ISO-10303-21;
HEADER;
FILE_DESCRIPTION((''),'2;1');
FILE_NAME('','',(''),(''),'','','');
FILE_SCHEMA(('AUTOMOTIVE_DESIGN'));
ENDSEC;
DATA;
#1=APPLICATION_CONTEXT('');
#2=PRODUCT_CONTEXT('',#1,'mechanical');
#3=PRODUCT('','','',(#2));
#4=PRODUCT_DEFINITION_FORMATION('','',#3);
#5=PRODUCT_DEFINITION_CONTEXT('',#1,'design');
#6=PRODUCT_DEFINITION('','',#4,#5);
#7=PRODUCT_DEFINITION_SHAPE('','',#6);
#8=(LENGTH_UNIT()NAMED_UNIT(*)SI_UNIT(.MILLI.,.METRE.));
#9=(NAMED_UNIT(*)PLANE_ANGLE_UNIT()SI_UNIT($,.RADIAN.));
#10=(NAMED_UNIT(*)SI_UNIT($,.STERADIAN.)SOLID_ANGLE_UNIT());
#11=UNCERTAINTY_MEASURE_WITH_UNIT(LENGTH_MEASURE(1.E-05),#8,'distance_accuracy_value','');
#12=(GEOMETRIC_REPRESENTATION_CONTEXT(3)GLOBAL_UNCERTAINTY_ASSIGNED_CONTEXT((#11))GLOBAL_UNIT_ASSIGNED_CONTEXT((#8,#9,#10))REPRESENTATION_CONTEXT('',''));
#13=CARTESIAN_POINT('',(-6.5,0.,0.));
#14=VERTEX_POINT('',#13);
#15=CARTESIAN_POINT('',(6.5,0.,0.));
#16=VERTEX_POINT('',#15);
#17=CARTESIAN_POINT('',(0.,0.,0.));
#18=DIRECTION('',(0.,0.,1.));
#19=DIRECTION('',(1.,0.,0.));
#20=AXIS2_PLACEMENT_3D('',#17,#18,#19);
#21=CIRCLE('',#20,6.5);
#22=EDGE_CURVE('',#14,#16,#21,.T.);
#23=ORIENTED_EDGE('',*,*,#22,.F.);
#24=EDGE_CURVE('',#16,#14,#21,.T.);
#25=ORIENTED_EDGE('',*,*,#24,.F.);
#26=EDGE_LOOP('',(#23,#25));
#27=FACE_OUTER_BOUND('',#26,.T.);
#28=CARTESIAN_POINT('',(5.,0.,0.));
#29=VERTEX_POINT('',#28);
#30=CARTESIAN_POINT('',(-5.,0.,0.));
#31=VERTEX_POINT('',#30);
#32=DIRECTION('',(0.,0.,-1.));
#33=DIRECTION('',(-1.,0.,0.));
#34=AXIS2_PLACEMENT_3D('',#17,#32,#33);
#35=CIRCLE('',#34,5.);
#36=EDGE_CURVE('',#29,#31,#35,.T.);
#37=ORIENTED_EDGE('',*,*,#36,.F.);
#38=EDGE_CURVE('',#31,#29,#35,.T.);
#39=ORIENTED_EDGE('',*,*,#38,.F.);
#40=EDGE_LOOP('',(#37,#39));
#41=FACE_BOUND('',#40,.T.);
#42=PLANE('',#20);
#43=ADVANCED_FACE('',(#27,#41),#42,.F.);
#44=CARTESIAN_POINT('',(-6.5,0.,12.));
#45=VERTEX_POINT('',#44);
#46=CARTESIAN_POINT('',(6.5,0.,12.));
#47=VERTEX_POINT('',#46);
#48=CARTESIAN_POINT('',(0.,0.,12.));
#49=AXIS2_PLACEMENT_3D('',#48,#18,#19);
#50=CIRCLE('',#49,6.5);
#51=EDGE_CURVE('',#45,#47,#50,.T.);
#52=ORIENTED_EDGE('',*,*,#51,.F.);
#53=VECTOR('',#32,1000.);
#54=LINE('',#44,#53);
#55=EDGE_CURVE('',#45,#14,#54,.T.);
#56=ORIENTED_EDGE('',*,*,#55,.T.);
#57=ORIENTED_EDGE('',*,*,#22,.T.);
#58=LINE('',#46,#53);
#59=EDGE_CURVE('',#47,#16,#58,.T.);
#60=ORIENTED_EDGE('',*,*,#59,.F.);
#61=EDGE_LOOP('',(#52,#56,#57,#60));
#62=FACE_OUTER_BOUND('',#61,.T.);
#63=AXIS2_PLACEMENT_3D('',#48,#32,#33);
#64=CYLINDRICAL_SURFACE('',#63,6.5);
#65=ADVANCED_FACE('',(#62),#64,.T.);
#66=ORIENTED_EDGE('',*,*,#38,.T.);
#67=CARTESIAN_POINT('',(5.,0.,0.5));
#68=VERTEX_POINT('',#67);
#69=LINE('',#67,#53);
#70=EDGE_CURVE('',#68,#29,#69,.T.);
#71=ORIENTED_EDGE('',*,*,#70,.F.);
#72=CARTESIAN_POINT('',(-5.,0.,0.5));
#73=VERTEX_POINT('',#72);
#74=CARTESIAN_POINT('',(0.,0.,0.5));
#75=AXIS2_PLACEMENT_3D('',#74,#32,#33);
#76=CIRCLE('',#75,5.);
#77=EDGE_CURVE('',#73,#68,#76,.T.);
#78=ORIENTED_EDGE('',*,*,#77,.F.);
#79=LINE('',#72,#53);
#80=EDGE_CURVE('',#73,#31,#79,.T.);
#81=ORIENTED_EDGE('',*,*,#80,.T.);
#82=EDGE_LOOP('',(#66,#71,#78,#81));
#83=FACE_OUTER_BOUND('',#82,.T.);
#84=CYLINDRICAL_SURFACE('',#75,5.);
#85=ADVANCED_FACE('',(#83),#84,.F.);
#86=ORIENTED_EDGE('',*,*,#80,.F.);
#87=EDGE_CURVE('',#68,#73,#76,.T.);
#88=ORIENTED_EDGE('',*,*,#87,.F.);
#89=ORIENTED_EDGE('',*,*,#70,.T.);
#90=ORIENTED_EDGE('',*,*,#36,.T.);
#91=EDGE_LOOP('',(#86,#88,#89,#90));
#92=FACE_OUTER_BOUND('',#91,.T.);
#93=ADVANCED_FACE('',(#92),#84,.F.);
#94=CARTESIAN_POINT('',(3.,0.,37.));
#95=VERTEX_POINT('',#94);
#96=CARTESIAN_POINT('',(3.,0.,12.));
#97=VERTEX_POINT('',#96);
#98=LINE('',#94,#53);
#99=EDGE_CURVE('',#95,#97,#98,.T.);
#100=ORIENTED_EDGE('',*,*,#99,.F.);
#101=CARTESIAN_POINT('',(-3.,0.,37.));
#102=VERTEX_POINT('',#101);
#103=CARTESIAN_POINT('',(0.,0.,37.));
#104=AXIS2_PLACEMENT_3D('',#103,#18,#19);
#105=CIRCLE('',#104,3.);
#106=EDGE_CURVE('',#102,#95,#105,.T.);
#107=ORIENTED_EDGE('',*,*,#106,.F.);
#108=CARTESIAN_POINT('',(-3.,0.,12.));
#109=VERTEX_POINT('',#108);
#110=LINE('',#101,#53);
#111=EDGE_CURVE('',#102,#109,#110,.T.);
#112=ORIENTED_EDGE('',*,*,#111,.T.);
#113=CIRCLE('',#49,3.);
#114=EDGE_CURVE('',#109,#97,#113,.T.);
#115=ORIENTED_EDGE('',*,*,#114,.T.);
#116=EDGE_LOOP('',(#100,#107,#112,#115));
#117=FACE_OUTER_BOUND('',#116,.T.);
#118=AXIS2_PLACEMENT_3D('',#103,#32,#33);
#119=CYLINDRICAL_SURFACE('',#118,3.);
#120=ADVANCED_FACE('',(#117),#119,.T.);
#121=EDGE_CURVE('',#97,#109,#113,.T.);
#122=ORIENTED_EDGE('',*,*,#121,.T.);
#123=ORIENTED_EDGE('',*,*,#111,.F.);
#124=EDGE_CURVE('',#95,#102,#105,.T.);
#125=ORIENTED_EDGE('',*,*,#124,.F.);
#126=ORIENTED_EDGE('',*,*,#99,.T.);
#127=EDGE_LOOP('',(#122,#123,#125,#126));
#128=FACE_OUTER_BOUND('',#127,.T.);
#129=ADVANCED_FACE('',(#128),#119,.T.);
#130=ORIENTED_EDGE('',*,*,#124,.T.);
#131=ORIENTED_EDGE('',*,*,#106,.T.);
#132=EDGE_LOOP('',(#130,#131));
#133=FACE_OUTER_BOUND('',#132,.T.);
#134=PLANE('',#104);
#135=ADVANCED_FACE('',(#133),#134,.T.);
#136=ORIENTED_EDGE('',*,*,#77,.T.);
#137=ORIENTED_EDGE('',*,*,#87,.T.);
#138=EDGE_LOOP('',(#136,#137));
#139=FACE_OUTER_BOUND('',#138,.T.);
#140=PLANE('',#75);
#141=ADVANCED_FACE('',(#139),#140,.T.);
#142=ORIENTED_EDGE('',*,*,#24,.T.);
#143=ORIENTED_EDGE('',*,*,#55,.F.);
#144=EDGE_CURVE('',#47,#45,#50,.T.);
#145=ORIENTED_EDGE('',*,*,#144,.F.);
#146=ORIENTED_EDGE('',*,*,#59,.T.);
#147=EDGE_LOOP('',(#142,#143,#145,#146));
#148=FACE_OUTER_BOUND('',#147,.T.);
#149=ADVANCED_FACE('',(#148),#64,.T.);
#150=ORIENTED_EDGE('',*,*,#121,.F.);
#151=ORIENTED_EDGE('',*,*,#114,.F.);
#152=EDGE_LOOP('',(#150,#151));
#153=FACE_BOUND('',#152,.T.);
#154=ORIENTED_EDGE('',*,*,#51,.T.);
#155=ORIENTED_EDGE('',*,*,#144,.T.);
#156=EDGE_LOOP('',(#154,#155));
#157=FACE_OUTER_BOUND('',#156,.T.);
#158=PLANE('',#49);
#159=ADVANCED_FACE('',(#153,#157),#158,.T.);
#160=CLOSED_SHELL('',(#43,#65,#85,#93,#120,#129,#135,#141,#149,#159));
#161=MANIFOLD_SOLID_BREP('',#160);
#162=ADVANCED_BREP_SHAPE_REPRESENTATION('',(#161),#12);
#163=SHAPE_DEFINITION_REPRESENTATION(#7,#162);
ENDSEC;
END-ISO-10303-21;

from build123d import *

# Parameters (mm, degrees)
SKETCH_1_R          = 6.5
EXTRUDE_1_DEPTH     = 12
SKETCH_2_R          = 3
EXTRUDE_2_DEPTH     = 25
SKETCH_3_R          = 5
CUT_EXTRUDE_1_DEPTH = 0.5


with BuildPart() as part:
    # 草图1 → 凸台-拉伸1 (new body)
    with BuildSketch(Plane.XY):
        Circle(SKETCH_1_R)
    extrude(amount=EXTRUDE_1_DEPTH)

    # 草图2 → 凸台-拉伸2 (add)
    with BuildSketch(Plane.XY.offset(12)):
        Circle(SKETCH_2_R)
    extrude(amount=EXTRUDE_2_DEPTH)

    # 草图3 → 切除-拉伸1 (cut)
    with BuildSketch(Plane(origin=(0, 0, 0), x_dir=(-1, 0, 0), z_dir=(0, 0, -1))):
        Circle(SKETCH_3_R)
    extrude(amount=-CUT_EXTRUDE_1_DEPTH, mode=Mode.SUBTRACT)


solid = part.part
